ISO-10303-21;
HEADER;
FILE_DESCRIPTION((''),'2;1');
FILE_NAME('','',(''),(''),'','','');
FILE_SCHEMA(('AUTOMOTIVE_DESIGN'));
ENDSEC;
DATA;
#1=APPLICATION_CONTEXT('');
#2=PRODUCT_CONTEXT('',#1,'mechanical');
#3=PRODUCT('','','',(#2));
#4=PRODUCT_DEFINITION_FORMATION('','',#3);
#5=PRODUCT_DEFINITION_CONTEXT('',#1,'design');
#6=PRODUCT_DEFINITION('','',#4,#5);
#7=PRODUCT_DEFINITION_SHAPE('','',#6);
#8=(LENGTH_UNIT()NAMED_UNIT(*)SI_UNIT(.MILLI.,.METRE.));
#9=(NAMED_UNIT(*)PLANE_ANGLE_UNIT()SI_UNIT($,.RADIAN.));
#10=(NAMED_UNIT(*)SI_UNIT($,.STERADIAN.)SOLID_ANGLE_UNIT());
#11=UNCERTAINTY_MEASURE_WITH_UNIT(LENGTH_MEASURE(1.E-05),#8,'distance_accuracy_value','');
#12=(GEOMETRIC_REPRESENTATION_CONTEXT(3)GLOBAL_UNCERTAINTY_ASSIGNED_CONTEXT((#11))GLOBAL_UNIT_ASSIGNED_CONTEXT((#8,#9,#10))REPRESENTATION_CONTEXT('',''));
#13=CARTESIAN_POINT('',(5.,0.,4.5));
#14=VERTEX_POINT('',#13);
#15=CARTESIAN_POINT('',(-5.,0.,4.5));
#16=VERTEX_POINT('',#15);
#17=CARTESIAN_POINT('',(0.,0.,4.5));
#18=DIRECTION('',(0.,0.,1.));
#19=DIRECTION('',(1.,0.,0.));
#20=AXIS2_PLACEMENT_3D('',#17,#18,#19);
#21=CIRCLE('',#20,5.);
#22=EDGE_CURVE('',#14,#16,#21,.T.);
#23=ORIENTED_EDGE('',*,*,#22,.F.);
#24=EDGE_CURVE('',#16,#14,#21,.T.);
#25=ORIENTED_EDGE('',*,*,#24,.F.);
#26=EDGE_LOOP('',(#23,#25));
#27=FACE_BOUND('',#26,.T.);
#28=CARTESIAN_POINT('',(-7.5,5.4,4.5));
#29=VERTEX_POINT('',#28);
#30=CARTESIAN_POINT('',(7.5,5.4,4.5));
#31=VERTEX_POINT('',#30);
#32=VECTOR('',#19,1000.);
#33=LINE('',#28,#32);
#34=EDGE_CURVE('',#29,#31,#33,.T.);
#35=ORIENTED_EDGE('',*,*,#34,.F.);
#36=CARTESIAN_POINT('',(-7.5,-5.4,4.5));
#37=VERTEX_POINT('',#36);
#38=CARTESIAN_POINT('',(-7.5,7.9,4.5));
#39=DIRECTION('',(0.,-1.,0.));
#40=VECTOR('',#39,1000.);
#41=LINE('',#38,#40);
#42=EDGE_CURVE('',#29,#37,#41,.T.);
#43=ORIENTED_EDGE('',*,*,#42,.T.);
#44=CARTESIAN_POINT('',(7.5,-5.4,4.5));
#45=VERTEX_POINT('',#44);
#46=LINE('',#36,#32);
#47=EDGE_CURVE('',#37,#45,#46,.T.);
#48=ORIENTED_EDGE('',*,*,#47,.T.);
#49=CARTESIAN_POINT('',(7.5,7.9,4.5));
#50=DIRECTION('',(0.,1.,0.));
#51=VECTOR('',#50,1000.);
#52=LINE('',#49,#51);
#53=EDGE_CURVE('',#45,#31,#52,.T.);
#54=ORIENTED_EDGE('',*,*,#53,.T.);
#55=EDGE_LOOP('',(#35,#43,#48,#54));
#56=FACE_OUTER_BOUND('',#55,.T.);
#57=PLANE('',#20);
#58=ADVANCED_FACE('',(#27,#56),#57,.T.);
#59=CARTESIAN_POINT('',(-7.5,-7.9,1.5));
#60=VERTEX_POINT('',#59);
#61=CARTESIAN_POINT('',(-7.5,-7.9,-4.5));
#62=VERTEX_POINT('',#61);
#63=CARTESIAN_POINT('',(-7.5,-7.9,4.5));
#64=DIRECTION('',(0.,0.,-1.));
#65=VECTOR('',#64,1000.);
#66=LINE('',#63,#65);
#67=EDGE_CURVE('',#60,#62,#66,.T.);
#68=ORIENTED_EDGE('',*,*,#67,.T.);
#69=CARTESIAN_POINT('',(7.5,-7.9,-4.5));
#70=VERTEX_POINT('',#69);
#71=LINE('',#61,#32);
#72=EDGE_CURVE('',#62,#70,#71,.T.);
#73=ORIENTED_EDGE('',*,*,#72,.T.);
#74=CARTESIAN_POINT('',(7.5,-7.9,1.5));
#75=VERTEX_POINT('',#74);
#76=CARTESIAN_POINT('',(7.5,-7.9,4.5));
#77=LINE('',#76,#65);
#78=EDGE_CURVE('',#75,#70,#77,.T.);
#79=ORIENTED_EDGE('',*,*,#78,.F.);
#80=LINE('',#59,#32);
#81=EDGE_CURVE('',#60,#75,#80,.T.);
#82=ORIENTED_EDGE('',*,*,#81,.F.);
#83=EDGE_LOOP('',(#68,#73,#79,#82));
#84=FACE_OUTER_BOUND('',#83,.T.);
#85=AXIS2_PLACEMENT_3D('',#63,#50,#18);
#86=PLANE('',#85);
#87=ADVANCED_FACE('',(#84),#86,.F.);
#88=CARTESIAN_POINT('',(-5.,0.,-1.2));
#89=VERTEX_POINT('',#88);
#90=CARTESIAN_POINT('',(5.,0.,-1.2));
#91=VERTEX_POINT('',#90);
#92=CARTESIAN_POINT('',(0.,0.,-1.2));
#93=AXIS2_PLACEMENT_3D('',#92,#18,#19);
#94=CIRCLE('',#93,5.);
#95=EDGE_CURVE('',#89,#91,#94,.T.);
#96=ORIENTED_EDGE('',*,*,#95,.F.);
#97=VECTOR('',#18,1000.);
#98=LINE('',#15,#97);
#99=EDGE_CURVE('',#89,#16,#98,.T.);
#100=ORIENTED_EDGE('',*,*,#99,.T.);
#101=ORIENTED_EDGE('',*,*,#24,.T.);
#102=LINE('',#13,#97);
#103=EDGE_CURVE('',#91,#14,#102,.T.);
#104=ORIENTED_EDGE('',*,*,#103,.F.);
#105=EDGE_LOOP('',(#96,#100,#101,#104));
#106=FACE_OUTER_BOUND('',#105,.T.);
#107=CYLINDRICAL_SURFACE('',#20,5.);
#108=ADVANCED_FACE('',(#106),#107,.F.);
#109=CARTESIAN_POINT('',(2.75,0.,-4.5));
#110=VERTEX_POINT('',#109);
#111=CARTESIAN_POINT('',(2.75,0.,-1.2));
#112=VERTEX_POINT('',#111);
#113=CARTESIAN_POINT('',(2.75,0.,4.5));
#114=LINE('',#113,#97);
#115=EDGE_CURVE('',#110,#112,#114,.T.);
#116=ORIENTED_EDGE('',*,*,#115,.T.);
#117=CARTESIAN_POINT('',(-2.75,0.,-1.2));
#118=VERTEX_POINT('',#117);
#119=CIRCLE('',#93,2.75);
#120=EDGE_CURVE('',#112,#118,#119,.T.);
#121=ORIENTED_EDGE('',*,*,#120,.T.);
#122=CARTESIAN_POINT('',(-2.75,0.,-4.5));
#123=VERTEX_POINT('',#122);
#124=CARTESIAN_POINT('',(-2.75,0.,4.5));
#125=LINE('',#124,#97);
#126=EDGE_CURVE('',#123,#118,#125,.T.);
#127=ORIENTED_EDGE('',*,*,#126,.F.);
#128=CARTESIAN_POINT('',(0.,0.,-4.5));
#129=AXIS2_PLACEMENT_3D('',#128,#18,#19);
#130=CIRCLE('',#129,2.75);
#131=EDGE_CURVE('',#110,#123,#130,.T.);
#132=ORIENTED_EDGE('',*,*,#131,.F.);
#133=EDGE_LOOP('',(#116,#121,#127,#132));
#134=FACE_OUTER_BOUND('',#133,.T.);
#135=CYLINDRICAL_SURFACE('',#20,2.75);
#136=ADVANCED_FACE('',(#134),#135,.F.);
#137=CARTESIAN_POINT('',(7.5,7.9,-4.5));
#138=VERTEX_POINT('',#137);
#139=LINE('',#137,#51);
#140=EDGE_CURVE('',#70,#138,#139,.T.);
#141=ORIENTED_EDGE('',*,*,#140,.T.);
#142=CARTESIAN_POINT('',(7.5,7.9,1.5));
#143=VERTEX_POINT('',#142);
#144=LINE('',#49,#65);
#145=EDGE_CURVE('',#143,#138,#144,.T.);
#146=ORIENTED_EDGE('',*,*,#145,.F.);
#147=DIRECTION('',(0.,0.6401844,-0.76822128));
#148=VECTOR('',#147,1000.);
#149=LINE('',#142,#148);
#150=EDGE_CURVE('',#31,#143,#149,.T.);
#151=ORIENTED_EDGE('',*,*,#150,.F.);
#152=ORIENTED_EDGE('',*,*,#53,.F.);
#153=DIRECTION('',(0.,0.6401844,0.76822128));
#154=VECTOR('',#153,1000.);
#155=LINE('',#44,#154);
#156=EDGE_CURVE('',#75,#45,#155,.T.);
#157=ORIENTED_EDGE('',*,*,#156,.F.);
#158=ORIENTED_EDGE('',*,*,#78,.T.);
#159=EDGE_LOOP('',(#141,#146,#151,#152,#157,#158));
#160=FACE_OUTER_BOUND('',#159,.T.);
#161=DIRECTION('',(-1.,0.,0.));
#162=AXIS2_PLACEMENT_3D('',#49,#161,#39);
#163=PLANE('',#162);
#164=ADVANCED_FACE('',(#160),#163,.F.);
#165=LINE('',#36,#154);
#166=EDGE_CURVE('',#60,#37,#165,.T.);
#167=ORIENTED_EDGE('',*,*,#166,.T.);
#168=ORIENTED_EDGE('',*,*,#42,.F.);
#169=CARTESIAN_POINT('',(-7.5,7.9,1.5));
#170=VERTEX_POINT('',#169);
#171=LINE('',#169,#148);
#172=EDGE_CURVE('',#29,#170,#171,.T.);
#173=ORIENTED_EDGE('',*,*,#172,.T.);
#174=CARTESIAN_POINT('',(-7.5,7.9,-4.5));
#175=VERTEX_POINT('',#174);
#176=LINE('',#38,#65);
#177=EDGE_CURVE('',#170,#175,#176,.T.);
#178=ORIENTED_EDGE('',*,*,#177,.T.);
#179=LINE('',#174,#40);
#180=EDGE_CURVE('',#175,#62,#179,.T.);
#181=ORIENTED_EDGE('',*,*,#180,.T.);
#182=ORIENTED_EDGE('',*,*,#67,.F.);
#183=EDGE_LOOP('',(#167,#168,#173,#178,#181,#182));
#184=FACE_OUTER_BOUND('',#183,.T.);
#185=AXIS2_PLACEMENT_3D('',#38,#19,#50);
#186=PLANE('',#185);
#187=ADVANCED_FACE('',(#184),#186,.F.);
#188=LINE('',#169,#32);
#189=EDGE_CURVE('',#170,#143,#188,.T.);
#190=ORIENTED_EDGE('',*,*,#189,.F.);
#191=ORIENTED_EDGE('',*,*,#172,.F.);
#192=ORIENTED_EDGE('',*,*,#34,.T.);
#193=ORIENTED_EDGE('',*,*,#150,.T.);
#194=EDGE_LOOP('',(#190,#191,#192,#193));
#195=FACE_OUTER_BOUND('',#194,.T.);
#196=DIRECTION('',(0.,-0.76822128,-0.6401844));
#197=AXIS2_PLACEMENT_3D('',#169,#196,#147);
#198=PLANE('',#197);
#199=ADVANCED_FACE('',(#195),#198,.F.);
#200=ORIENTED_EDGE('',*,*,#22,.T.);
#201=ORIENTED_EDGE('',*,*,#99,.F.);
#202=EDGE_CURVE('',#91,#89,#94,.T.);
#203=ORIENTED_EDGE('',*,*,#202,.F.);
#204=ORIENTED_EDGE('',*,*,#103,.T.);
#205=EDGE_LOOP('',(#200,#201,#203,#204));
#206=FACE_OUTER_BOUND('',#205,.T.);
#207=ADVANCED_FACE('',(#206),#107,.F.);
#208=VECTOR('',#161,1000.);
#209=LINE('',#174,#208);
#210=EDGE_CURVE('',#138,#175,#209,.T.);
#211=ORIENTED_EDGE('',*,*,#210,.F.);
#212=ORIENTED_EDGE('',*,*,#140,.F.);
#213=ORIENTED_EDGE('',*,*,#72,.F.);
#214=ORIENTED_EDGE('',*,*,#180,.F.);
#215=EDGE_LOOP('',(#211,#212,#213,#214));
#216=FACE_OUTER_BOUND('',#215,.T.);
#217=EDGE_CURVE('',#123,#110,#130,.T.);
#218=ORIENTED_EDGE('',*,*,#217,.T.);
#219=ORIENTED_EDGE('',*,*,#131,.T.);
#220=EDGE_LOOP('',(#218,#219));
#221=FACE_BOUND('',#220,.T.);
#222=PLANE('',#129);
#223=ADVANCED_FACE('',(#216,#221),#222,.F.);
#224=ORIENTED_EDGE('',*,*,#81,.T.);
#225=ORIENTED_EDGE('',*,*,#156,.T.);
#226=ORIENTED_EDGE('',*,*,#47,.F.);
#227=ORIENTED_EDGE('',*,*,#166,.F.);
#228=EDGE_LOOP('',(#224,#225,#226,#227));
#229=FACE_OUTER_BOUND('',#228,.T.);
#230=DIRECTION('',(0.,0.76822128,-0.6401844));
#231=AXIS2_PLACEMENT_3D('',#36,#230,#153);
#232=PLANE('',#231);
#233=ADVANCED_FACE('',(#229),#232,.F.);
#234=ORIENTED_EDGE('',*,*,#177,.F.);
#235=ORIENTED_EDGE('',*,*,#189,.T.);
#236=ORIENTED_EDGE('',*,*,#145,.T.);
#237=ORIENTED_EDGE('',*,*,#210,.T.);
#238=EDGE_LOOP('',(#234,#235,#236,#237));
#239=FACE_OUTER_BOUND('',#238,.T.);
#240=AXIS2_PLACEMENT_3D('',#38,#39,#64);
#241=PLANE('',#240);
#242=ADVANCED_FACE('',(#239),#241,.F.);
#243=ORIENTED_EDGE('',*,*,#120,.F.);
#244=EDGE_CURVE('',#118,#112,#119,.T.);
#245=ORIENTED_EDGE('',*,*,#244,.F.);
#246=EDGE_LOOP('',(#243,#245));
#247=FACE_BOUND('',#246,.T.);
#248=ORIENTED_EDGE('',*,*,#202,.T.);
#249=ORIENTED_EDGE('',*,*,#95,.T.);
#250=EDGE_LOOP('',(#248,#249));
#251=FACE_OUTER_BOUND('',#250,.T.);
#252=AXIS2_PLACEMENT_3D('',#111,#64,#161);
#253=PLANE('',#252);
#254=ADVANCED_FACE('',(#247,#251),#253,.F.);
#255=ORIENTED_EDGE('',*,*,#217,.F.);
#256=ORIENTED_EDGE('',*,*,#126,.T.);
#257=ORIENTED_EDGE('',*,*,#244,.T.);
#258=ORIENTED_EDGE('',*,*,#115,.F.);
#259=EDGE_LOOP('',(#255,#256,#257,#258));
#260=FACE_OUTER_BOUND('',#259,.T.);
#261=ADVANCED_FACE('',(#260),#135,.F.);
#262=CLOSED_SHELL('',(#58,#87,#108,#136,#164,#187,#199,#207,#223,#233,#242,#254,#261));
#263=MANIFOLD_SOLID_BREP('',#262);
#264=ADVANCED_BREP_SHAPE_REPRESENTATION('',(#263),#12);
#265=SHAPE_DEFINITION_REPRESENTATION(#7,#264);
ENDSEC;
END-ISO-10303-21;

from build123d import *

# Parameters (mm, degrees)
SKETCH_1_W                   = 15
SKETCH_1_H                   = 15.8
EXTRUDE_1_DEPTH              = 4.5
HOLE_WIZARD_M4_1_D           = 5.5
HOLE_WIZARD_M4_1_CBORE_D     = 10
HOLE_WIZARD_M4_1_CBORE_DEPTH = 5.7
CUT_EXTRUDE_1_DEPTH          = 18.540239451


with BuildPart() as part:
    # 草图1 → 凸台-拉伸1 (new, symmetric)
    with BuildSketch(Plane.XY):
        Rectangle(SKETCH_1_W, SKETCH_1_H)
    extrude(amount=EXTRUDE_1_DEPTH, both=True)

    # M4 沉头孔1 (through all)
    with Locations(Plane.XY.offset(4.5)):
        with Locations((0, 0)):
            CounterBoreHole(HOLE_WIZARD_M4_1_D / 2, HOLE_WIZARD_M4_1_CBORE_D / 2, HOLE_WIZARD_M4_1_CBORE_DEPTH)

    # 草图4 → 切除-拉伸1 (cut, through all)
    with BuildSketch(Plane(origin=(7.5, 0, 0), x_dir=(0, 0, -1), z_dir=(1, 0, 0))):
        Polygon((-4.5, -7.9), (-4.5, -5.4), (-1.5, -7.9), align=None)
        Polygon((-4.5, 5.4), (-4.5, 7.9), (-1.5, 7.9), align=None)
    extrude(amount=-CUT_EXTRUDE_1_DEPTH, mode=Mode.SUBTRACT)


solid = part.part
